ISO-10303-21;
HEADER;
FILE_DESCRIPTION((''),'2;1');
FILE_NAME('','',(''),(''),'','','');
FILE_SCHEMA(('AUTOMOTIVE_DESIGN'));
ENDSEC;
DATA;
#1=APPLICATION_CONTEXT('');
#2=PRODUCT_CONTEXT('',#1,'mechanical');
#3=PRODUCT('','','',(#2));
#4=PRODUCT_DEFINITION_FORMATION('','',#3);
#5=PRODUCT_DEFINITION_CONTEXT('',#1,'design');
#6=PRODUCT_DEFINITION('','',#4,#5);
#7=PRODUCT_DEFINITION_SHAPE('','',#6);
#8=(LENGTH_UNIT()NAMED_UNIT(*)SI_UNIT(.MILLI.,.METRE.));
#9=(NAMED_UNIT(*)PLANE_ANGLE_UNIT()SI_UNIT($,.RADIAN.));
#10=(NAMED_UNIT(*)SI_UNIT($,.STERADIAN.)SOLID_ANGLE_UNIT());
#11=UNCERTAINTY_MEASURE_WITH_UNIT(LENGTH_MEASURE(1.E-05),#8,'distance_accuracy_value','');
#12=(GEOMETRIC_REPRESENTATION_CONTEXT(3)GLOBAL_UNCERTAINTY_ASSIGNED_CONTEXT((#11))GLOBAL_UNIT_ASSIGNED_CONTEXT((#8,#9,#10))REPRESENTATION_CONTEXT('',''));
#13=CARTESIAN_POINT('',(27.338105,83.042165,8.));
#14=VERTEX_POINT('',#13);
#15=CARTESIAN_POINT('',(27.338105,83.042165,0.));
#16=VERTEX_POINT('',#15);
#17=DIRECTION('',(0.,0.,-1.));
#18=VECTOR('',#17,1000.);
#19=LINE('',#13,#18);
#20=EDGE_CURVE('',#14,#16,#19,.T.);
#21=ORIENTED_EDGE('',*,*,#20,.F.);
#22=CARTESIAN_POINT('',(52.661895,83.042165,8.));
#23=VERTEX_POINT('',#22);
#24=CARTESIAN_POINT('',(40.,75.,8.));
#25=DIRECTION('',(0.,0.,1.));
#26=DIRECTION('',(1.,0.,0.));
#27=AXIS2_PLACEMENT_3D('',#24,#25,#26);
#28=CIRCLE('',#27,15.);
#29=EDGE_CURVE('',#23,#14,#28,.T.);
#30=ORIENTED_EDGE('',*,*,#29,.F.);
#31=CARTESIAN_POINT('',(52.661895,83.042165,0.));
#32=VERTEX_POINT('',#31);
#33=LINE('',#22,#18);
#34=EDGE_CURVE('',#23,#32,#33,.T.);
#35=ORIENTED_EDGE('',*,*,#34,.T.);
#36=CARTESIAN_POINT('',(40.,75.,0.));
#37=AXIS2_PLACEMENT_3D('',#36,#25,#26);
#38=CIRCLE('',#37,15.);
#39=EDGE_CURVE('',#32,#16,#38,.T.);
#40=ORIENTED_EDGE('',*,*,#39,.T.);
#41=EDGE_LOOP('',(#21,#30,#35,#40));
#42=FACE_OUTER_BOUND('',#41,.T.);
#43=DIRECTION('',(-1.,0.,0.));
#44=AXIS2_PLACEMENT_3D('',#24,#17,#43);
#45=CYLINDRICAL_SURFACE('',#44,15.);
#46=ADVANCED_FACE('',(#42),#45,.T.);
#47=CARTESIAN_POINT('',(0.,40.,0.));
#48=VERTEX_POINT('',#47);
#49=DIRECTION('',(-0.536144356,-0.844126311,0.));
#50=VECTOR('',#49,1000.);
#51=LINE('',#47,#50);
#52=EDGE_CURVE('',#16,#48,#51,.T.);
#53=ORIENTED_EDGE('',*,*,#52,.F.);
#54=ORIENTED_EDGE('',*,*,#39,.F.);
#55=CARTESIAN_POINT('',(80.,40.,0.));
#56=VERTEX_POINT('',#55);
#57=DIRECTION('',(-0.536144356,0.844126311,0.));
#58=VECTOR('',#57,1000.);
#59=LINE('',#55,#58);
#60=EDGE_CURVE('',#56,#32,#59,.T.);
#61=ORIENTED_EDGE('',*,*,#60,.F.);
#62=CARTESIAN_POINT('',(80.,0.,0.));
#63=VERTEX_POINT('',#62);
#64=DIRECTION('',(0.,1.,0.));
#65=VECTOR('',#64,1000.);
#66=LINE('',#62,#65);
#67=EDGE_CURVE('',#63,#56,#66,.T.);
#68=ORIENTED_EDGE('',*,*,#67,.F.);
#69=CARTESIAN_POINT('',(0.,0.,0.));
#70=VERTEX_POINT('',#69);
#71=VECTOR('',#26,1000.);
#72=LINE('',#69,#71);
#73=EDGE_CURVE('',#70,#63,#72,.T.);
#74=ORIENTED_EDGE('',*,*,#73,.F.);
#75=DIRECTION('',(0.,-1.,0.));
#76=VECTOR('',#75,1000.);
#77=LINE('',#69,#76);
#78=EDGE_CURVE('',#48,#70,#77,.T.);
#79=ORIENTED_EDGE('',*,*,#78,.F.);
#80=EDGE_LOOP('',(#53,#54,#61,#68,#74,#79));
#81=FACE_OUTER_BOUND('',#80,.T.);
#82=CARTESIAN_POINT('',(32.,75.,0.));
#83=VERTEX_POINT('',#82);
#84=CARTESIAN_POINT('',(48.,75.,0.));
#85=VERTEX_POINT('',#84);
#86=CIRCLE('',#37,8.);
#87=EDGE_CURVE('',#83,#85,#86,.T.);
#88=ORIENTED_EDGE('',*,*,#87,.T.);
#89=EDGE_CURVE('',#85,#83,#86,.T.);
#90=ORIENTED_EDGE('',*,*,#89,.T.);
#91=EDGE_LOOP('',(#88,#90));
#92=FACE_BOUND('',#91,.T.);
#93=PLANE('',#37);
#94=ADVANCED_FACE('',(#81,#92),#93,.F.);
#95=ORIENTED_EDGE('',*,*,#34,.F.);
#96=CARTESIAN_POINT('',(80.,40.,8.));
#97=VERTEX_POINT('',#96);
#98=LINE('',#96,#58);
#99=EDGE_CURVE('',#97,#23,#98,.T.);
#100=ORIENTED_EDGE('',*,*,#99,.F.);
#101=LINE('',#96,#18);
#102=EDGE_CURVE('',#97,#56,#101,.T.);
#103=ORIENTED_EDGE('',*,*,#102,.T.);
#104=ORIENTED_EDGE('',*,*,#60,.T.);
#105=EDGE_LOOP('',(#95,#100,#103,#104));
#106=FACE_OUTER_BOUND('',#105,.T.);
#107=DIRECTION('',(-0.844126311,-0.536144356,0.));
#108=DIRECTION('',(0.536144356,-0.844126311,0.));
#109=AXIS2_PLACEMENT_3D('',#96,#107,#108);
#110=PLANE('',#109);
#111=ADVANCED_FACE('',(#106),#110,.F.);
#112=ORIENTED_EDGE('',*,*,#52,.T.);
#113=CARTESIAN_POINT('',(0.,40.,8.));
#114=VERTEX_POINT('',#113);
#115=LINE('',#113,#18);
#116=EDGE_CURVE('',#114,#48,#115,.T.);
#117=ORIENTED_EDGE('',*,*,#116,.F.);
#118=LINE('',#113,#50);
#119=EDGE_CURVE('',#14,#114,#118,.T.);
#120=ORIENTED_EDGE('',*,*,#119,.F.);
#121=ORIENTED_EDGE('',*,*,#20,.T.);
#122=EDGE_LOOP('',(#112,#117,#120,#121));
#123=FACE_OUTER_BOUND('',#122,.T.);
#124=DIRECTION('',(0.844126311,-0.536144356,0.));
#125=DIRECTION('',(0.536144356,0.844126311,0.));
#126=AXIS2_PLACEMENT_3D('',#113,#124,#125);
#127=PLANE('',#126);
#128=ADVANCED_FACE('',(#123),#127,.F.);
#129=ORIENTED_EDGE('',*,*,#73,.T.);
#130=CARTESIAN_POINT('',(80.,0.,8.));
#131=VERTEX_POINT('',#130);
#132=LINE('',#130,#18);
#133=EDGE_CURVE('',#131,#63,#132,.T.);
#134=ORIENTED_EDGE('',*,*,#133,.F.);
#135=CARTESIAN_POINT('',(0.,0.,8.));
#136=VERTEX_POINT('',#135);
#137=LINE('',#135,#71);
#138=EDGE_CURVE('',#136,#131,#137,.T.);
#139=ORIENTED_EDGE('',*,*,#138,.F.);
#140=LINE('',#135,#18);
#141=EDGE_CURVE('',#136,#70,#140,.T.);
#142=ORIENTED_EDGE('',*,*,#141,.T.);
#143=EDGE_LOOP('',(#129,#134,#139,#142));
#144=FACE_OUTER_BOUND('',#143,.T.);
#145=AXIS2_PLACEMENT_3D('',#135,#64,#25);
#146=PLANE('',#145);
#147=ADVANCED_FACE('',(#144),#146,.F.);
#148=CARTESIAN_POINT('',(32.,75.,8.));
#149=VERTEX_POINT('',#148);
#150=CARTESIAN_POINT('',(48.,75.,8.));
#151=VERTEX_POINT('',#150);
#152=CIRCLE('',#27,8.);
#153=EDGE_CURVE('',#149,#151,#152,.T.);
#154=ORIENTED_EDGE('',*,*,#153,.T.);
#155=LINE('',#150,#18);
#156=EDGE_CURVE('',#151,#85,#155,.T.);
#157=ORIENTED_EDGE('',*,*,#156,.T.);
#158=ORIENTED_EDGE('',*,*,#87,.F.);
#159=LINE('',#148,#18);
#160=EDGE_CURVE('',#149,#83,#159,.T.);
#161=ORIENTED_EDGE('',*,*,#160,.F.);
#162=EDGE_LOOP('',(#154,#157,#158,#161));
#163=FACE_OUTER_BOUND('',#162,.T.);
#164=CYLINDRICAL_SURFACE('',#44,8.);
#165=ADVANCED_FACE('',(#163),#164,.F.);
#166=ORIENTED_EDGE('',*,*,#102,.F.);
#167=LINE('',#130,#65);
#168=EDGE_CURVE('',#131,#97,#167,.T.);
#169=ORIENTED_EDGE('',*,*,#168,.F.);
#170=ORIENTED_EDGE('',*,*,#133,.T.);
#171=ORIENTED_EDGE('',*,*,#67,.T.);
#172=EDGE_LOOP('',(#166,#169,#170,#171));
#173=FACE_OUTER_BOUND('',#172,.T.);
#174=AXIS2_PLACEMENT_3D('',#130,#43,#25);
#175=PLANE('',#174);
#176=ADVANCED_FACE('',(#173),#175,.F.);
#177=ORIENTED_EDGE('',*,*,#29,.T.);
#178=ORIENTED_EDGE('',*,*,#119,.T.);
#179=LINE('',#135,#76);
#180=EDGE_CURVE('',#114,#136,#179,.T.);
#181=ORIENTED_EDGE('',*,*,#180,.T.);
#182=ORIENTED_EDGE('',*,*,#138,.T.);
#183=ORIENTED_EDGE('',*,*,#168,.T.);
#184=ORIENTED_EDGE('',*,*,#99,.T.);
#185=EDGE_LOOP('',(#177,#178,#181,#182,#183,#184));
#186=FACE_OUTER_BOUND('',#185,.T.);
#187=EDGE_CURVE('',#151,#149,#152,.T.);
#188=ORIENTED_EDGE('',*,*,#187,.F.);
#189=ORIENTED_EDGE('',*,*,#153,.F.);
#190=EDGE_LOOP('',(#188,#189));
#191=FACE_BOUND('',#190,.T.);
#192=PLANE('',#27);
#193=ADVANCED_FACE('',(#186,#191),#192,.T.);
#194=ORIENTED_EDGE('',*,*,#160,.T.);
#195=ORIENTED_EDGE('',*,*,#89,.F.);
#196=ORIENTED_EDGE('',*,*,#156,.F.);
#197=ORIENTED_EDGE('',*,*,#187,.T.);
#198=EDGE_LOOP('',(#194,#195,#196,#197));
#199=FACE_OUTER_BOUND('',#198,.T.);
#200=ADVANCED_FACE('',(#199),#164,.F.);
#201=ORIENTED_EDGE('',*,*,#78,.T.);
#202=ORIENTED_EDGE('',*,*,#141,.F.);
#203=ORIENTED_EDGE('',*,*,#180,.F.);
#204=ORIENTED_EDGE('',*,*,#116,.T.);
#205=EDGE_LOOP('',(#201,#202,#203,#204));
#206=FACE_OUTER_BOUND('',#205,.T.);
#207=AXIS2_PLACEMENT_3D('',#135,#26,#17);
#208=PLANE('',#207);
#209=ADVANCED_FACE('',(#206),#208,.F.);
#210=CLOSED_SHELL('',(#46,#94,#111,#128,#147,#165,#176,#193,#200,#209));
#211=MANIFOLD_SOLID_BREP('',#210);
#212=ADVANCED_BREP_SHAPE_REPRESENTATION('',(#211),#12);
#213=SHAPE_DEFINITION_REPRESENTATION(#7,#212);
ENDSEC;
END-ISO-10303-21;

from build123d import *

# Parameters (mm, degrees)
SKETCH1_R           = 8
BOSS_EXTRUDE1_DEPTH = 8


with BuildPart() as part:
    # Sketch1 → Boss-Extrude1 (new body)
    with BuildSketch(Plane.XY):
        with BuildLine():
            Line((0, 0), (0, 40))
            Line((0, 40), (27.338105329, 83.042165339))
            ThreePointArc((27.338105329, 83.042165339), (40, 90), (52.661894671, 83.042165339))
            Line((52.661894671, 83.042165339), (80, 40))
            Line((80, 40), (80, 0))
            Line((80, 0), (0, 0))
        make_face()
        with Locations((40, 75)):
            Circle(SKETCH1_R, mode=Mode.SUBTRACT)
    extrude(amount=BOSS_EXTRUDE1_DEPTH)


solid = part.part
